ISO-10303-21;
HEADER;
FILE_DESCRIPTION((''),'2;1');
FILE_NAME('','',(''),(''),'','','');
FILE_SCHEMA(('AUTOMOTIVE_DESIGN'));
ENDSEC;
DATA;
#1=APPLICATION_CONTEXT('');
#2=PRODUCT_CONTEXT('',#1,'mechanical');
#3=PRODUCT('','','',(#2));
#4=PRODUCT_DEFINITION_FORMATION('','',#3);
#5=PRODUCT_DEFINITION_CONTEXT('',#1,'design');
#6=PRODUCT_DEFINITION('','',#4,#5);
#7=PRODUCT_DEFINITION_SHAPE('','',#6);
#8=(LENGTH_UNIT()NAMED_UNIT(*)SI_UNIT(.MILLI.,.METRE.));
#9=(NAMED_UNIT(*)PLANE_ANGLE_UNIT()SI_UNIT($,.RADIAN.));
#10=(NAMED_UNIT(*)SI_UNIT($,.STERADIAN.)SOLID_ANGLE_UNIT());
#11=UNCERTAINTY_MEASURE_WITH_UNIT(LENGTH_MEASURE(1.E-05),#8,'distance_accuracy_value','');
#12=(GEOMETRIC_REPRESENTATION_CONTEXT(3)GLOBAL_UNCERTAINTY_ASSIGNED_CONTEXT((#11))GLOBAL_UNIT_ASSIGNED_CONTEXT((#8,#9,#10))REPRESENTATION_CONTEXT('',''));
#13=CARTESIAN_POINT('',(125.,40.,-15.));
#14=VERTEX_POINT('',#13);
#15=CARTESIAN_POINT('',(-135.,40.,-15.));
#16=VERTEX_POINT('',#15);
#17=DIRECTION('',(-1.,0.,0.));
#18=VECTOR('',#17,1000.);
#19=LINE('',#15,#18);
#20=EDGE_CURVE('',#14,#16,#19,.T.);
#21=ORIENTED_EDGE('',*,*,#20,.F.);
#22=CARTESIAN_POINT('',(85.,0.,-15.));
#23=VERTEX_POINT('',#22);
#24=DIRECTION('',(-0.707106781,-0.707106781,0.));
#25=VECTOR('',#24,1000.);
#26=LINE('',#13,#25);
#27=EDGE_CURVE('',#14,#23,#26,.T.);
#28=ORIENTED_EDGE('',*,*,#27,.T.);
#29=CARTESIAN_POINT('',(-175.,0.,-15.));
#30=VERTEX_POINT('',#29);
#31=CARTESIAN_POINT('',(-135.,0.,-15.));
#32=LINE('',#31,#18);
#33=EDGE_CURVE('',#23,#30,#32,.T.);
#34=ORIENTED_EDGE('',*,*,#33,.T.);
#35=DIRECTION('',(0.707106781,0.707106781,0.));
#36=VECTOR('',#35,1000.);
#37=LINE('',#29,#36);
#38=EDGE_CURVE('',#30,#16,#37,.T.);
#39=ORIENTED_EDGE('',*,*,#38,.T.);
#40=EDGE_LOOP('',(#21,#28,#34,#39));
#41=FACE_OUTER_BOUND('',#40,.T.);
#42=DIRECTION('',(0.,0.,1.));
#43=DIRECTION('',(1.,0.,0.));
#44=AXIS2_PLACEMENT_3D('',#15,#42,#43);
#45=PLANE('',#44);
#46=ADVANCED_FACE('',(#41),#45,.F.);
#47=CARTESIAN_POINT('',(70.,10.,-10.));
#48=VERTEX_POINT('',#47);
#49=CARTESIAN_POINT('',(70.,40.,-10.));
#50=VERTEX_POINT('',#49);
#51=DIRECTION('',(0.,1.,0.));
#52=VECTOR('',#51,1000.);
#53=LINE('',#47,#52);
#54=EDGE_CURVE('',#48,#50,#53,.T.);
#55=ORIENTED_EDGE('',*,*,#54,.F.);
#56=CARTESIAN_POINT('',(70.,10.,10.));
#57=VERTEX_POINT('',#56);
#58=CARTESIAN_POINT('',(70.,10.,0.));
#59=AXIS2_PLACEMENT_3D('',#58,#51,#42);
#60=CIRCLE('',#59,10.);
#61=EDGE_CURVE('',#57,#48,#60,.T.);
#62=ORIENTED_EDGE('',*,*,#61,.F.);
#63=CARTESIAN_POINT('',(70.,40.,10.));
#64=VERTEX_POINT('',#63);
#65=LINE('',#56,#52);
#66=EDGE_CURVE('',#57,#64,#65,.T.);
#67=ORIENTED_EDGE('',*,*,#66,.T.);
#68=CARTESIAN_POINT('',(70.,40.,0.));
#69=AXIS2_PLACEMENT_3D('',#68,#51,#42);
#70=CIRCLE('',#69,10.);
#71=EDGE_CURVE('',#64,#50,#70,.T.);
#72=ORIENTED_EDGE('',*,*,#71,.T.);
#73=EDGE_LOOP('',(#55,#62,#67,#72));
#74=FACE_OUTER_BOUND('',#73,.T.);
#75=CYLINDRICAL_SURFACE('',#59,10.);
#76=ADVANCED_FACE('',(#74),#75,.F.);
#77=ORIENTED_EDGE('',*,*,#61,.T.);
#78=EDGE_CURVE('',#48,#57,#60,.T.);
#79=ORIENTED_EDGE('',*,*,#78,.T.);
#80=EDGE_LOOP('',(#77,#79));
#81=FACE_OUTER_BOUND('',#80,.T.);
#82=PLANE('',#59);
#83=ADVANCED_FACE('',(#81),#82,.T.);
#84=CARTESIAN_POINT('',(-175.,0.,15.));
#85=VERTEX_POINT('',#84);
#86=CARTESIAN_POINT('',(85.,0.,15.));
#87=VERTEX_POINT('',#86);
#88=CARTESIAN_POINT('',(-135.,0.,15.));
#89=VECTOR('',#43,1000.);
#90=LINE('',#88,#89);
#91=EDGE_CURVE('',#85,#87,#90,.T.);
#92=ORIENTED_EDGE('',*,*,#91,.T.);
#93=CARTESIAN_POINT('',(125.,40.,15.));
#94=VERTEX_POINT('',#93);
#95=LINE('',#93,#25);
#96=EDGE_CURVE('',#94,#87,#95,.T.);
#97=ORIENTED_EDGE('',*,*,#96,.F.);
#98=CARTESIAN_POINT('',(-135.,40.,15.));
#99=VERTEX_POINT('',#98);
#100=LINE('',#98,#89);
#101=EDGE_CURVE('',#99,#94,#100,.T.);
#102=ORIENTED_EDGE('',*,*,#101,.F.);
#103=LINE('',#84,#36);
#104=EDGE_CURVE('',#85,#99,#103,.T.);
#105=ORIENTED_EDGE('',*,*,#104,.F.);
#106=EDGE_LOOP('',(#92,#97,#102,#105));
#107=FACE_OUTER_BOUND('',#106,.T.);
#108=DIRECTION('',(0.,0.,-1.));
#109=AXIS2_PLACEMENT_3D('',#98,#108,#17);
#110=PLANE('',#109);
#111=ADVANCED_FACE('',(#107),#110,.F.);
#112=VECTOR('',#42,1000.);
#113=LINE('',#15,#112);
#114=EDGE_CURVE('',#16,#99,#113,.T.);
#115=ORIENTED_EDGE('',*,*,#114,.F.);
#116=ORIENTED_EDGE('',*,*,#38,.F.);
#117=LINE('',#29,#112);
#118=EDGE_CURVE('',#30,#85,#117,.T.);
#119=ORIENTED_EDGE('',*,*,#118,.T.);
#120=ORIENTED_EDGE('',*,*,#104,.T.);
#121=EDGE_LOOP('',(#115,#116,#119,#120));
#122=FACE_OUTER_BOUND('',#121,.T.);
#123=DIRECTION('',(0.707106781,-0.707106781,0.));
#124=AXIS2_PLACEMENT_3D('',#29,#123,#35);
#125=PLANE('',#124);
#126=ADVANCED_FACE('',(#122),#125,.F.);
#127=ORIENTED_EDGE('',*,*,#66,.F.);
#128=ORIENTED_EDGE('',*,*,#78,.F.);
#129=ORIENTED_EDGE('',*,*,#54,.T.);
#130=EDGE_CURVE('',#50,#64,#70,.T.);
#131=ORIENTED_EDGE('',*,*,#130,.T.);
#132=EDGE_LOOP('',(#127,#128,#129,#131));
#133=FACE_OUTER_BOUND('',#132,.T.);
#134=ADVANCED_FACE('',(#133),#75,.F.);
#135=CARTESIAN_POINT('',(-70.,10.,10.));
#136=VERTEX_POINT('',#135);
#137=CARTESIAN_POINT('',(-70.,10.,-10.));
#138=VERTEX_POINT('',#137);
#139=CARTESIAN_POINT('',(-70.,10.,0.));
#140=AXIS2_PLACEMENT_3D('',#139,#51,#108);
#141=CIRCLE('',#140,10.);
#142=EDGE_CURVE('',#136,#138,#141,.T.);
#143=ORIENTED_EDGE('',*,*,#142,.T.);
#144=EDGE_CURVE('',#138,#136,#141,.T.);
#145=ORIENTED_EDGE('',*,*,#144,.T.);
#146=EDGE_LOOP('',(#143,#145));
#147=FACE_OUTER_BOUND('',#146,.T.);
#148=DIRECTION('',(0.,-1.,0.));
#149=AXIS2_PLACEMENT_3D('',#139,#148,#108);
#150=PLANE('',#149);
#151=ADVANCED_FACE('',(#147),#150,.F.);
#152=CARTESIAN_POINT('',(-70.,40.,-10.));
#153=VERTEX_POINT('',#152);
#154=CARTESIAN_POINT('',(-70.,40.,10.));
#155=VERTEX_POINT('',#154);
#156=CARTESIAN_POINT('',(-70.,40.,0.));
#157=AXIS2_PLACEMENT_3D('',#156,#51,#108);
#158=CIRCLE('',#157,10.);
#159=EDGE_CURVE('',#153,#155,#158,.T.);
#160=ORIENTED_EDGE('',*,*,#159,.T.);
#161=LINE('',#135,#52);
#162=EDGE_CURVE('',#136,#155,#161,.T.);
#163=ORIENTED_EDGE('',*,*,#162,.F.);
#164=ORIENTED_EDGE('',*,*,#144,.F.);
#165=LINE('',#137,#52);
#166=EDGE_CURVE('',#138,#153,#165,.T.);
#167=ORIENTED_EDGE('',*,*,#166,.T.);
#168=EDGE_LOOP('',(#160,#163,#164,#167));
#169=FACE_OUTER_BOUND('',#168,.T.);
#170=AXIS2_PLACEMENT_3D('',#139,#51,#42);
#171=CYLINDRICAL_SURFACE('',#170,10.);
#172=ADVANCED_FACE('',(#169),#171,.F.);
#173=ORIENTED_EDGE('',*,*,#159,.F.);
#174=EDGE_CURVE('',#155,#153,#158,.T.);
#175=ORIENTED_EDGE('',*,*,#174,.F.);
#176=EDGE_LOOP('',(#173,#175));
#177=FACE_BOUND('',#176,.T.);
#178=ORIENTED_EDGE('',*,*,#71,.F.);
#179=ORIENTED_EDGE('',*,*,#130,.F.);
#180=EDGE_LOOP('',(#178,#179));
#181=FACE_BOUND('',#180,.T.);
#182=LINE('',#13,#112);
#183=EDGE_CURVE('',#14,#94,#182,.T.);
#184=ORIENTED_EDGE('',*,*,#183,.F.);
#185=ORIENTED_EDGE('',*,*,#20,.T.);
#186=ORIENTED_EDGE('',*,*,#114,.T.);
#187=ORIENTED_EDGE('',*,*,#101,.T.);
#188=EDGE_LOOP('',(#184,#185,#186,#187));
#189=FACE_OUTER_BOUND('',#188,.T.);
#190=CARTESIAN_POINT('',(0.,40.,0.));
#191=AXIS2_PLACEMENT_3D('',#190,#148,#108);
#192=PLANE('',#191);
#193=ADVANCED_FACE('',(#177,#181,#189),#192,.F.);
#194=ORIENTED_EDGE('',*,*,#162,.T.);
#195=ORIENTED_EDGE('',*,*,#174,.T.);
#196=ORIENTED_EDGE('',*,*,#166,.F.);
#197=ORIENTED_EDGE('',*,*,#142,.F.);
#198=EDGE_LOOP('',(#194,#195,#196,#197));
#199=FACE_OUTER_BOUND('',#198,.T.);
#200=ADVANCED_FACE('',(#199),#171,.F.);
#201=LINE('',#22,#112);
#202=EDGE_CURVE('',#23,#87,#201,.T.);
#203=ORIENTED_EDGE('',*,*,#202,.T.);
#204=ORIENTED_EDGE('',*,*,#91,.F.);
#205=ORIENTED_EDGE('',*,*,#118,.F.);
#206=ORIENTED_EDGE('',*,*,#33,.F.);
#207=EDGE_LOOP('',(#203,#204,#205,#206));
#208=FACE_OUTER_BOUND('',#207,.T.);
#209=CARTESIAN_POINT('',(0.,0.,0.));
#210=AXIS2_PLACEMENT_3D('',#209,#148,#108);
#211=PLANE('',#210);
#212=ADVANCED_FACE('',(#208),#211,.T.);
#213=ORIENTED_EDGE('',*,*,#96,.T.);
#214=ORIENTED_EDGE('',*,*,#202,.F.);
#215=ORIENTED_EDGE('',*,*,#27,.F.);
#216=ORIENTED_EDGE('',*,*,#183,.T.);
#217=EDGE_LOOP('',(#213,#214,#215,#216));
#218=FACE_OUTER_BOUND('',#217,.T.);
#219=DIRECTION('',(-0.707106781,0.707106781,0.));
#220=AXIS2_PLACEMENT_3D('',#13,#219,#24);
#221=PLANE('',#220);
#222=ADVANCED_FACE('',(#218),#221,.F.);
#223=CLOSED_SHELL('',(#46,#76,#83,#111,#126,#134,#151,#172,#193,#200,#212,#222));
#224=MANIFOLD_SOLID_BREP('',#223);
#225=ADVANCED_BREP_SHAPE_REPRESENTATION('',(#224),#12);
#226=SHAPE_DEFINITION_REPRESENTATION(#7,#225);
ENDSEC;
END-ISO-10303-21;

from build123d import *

# Parameters (mm, degrees)
SKETCH_1_W          = 270
SKETCH_1_H          = 30
EXTRUDE_1_DEPTH     = 40
SKETCH_2_R          = 10
CUT_EXTRUDE_2_DEPTH = 30
SKETCH_7_W          = 30
SKETCH_7_H          = 40
CUT_EXTRUDE_5_DEPTH = 10
CUT_EXTRUDE_6_DEPTH = 144.961800489
SKETCH_5_W          = 30
SKETCH_5_H          = 40
EXTRUDE_3_DEPTH     = 40
CUT_EXTRUDE_4_DEPTH = 183.002747232


with BuildPart() as part:
    # 草图1 → 凸台-拉伸1 (new body)
    with BuildSketch(Plane(origin=(0, 0, 0), x_dir=(1, 0, 0), z_dir=(0, 1, 0))):
        Rectangle(SKETCH_1_W, SKETCH_1_H)
    extrude(amount=EXTRUDE_1_DEPTH)

    # 草图2 → 切除-拉伸2 (cut)
    with BuildSketch(Plane(origin=(0, 40, 0), x_dir=(1, 0, 0), z_dir=(0, 1, 0))):
        with Locations(Location((70, 0, 0), (0, 0, 270))):
            Circle(SKETCH_2_R)
        with Locations(Location((-70, 0, 0), (0, 0, 90))):
            Circle(SKETCH_2_R)
    extrude(amount=-CUT_EXTRUDE_2_DEPTH, mode=Mode.SUBTRACT)

    # 草图7 → 切除-拉伸5 (cut)
    with BuildSketch(Plane(origin=(135, 0, 0), x_dir=(0, 0, -1), z_dir=(1, 0, 0))):
        with Locations((0, 20)):
            Rectangle(SKETCH_7_W, SKETCH_7_H)
    extrude(amount=-CUT_EXTRUDE_5_DEPTH, mode=Mode.SUBTRACT)

    # 草图8 → 切除-拉伸6 (cut, through all)
    with BuildSketch(Plane.XY.offset(15)):
        Polygon((125, 40), (85, 0), (125, 0), align=None)
    extrude(amount=-CUT_EXTRUDE_6_DEPTH, mode=Mode.SUBTRACT)

    # 草图5 → 凸台-拉伸3 (add)
    with BuildSketch(Plane.ZY.offset(135)):
        with Locations((0, 20)):
            Rectangle(SKETCH_5_W, SKETCH_5_H)
    extrude(amount=EXTRUDE_3_DEPTH)

    # 草图6 → 切除-拉伸4 (cut, through all)
    with BuildSketch(Plane.XY.offset(15)):
        Polygon((-175, 0), (-135, 40), (-175, 40), align=None)
    extrude(amount=-CUT_EXTRUDE_4_DEPTH, mode=Mode.SUBTRACT)


solid = part.part
